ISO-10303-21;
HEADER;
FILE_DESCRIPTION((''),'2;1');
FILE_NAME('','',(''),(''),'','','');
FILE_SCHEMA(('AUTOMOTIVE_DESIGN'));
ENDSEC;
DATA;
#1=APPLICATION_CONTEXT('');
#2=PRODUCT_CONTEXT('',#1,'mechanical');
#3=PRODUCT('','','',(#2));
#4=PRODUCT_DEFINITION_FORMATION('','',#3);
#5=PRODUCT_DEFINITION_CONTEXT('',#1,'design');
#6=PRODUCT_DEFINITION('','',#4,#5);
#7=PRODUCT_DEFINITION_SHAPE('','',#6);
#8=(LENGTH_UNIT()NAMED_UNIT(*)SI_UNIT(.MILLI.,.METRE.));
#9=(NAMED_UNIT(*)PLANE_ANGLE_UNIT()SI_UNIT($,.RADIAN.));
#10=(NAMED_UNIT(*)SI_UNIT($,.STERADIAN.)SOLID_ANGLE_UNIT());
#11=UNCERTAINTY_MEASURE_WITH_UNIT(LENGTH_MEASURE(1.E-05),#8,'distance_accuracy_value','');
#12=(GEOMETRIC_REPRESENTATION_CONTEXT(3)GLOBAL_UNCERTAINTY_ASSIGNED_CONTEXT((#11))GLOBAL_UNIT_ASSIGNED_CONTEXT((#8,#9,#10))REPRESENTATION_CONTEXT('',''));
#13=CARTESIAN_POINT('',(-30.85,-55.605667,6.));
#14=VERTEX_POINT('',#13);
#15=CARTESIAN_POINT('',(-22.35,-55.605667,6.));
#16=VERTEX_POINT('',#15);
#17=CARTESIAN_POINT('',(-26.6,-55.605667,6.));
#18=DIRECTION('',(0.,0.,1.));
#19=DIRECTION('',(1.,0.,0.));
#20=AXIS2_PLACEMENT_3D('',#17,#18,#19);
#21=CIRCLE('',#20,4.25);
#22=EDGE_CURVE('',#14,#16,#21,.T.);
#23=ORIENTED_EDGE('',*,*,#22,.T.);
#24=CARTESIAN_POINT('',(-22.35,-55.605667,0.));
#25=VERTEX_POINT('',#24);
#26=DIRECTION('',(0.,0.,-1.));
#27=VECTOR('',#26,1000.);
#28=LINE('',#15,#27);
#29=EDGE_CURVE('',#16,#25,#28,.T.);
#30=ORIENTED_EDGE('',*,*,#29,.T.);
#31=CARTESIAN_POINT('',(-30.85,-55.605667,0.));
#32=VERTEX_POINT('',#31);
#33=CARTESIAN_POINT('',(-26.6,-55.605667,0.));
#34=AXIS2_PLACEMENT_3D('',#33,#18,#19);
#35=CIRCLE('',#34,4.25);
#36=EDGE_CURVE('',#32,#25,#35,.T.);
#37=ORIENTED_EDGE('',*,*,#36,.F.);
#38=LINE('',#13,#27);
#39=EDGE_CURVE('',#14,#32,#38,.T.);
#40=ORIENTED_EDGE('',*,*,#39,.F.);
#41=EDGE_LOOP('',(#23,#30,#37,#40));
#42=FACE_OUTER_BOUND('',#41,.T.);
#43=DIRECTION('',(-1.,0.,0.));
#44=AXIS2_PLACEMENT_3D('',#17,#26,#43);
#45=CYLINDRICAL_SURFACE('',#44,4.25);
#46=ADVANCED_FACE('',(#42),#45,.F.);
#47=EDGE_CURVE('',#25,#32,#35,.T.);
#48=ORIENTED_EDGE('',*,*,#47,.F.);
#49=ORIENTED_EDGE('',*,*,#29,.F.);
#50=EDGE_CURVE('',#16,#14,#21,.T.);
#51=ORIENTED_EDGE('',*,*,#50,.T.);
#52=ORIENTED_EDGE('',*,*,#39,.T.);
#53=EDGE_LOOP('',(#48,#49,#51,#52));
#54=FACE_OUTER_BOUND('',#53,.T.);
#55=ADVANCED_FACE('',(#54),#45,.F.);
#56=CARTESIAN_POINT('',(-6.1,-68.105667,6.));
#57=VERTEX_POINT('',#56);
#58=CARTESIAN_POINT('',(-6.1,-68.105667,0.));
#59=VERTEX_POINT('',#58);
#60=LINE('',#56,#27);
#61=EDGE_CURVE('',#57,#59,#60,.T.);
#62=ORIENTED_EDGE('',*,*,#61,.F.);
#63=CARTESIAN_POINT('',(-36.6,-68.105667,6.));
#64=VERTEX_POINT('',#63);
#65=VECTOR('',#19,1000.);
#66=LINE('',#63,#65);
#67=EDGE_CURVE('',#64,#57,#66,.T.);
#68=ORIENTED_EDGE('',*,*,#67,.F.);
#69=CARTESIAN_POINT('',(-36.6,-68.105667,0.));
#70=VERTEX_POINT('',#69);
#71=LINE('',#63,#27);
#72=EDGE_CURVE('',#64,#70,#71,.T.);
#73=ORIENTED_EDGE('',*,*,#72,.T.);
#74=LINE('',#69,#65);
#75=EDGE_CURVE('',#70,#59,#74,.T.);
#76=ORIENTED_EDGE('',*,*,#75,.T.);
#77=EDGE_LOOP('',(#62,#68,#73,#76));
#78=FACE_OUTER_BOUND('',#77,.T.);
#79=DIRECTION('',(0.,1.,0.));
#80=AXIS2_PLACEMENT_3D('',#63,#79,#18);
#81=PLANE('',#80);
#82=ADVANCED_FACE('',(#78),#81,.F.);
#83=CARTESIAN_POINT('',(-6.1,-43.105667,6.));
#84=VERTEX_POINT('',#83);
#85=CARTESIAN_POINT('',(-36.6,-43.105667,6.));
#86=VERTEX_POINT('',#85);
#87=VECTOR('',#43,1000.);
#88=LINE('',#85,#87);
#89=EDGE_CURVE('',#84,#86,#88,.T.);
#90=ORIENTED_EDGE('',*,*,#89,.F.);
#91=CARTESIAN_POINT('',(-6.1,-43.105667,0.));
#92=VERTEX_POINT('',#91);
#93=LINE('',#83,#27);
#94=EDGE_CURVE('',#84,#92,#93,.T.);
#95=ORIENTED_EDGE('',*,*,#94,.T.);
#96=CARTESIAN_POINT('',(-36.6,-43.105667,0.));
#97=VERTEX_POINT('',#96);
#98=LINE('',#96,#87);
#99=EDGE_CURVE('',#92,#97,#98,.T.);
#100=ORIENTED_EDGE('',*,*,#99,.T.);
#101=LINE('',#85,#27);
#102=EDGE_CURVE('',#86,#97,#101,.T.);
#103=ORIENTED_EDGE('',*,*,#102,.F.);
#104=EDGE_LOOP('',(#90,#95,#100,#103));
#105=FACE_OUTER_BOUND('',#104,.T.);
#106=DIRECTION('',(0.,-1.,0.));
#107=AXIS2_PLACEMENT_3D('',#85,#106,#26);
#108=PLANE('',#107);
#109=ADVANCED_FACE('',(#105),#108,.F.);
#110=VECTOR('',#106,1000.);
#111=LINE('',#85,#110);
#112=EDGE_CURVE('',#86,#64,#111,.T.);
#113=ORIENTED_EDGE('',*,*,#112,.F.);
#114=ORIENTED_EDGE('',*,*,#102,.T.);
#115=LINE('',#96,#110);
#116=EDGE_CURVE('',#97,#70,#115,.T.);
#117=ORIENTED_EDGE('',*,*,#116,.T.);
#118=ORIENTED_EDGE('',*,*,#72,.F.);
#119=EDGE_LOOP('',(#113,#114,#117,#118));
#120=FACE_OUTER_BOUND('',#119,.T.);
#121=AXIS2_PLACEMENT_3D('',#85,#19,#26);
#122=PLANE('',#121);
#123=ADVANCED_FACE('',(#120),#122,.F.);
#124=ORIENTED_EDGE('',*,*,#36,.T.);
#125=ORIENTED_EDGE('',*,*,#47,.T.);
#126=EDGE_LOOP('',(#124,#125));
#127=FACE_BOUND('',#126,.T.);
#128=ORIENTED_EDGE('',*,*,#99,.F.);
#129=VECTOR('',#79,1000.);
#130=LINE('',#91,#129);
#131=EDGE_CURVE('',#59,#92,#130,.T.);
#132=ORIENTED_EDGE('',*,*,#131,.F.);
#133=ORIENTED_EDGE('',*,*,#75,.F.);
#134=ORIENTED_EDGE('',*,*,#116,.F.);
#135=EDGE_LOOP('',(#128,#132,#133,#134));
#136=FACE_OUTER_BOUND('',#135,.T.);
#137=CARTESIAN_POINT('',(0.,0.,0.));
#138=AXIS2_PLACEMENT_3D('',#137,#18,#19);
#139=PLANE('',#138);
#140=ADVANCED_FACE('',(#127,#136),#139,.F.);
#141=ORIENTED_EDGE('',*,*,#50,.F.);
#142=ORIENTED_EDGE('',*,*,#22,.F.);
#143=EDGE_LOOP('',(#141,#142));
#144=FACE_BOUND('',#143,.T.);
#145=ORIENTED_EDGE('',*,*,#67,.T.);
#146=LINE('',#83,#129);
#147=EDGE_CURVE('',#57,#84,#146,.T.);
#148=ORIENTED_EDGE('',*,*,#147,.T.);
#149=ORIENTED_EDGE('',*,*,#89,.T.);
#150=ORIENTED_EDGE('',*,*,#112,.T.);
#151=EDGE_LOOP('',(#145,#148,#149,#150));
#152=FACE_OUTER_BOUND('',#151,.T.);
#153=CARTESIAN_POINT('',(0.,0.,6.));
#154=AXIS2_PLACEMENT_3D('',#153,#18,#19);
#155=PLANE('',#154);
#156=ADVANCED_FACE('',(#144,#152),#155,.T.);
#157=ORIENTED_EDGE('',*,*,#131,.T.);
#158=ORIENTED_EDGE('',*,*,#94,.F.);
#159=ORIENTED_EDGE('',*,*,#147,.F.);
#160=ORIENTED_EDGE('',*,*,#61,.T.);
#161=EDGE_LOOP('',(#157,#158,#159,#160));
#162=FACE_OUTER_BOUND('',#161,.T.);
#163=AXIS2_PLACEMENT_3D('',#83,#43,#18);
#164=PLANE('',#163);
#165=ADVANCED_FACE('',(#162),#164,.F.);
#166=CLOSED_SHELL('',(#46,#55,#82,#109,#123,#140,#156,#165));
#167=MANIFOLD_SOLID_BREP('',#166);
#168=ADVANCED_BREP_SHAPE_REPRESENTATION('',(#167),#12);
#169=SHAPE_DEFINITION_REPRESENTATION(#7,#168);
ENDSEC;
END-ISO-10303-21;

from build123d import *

# Parameters (mm, degrees)
SKETCH1_W           = 30.5
SKETCH1_H           = 25
SKETCH1_R           = 4.25
BOSS_EXTRUDE1_DEPTH = 6


with BuildPart() as part:
    # Sketch1 → Boss-Extrude1 (new body)
    with BuildSketch(Plane.XY):
        with Locations((-21.35, -55.605666667)):
            Rectangle(SKETCH1_W, SKETCH1_H)
        with Locations((-26.6, -55.605666667)):
            Circle(SKETCH1_R, mode=Mode.SUBTRACT)
    extrude(amount=BOSS_EXTRUDE1_DEPTH)


solid = part.part
